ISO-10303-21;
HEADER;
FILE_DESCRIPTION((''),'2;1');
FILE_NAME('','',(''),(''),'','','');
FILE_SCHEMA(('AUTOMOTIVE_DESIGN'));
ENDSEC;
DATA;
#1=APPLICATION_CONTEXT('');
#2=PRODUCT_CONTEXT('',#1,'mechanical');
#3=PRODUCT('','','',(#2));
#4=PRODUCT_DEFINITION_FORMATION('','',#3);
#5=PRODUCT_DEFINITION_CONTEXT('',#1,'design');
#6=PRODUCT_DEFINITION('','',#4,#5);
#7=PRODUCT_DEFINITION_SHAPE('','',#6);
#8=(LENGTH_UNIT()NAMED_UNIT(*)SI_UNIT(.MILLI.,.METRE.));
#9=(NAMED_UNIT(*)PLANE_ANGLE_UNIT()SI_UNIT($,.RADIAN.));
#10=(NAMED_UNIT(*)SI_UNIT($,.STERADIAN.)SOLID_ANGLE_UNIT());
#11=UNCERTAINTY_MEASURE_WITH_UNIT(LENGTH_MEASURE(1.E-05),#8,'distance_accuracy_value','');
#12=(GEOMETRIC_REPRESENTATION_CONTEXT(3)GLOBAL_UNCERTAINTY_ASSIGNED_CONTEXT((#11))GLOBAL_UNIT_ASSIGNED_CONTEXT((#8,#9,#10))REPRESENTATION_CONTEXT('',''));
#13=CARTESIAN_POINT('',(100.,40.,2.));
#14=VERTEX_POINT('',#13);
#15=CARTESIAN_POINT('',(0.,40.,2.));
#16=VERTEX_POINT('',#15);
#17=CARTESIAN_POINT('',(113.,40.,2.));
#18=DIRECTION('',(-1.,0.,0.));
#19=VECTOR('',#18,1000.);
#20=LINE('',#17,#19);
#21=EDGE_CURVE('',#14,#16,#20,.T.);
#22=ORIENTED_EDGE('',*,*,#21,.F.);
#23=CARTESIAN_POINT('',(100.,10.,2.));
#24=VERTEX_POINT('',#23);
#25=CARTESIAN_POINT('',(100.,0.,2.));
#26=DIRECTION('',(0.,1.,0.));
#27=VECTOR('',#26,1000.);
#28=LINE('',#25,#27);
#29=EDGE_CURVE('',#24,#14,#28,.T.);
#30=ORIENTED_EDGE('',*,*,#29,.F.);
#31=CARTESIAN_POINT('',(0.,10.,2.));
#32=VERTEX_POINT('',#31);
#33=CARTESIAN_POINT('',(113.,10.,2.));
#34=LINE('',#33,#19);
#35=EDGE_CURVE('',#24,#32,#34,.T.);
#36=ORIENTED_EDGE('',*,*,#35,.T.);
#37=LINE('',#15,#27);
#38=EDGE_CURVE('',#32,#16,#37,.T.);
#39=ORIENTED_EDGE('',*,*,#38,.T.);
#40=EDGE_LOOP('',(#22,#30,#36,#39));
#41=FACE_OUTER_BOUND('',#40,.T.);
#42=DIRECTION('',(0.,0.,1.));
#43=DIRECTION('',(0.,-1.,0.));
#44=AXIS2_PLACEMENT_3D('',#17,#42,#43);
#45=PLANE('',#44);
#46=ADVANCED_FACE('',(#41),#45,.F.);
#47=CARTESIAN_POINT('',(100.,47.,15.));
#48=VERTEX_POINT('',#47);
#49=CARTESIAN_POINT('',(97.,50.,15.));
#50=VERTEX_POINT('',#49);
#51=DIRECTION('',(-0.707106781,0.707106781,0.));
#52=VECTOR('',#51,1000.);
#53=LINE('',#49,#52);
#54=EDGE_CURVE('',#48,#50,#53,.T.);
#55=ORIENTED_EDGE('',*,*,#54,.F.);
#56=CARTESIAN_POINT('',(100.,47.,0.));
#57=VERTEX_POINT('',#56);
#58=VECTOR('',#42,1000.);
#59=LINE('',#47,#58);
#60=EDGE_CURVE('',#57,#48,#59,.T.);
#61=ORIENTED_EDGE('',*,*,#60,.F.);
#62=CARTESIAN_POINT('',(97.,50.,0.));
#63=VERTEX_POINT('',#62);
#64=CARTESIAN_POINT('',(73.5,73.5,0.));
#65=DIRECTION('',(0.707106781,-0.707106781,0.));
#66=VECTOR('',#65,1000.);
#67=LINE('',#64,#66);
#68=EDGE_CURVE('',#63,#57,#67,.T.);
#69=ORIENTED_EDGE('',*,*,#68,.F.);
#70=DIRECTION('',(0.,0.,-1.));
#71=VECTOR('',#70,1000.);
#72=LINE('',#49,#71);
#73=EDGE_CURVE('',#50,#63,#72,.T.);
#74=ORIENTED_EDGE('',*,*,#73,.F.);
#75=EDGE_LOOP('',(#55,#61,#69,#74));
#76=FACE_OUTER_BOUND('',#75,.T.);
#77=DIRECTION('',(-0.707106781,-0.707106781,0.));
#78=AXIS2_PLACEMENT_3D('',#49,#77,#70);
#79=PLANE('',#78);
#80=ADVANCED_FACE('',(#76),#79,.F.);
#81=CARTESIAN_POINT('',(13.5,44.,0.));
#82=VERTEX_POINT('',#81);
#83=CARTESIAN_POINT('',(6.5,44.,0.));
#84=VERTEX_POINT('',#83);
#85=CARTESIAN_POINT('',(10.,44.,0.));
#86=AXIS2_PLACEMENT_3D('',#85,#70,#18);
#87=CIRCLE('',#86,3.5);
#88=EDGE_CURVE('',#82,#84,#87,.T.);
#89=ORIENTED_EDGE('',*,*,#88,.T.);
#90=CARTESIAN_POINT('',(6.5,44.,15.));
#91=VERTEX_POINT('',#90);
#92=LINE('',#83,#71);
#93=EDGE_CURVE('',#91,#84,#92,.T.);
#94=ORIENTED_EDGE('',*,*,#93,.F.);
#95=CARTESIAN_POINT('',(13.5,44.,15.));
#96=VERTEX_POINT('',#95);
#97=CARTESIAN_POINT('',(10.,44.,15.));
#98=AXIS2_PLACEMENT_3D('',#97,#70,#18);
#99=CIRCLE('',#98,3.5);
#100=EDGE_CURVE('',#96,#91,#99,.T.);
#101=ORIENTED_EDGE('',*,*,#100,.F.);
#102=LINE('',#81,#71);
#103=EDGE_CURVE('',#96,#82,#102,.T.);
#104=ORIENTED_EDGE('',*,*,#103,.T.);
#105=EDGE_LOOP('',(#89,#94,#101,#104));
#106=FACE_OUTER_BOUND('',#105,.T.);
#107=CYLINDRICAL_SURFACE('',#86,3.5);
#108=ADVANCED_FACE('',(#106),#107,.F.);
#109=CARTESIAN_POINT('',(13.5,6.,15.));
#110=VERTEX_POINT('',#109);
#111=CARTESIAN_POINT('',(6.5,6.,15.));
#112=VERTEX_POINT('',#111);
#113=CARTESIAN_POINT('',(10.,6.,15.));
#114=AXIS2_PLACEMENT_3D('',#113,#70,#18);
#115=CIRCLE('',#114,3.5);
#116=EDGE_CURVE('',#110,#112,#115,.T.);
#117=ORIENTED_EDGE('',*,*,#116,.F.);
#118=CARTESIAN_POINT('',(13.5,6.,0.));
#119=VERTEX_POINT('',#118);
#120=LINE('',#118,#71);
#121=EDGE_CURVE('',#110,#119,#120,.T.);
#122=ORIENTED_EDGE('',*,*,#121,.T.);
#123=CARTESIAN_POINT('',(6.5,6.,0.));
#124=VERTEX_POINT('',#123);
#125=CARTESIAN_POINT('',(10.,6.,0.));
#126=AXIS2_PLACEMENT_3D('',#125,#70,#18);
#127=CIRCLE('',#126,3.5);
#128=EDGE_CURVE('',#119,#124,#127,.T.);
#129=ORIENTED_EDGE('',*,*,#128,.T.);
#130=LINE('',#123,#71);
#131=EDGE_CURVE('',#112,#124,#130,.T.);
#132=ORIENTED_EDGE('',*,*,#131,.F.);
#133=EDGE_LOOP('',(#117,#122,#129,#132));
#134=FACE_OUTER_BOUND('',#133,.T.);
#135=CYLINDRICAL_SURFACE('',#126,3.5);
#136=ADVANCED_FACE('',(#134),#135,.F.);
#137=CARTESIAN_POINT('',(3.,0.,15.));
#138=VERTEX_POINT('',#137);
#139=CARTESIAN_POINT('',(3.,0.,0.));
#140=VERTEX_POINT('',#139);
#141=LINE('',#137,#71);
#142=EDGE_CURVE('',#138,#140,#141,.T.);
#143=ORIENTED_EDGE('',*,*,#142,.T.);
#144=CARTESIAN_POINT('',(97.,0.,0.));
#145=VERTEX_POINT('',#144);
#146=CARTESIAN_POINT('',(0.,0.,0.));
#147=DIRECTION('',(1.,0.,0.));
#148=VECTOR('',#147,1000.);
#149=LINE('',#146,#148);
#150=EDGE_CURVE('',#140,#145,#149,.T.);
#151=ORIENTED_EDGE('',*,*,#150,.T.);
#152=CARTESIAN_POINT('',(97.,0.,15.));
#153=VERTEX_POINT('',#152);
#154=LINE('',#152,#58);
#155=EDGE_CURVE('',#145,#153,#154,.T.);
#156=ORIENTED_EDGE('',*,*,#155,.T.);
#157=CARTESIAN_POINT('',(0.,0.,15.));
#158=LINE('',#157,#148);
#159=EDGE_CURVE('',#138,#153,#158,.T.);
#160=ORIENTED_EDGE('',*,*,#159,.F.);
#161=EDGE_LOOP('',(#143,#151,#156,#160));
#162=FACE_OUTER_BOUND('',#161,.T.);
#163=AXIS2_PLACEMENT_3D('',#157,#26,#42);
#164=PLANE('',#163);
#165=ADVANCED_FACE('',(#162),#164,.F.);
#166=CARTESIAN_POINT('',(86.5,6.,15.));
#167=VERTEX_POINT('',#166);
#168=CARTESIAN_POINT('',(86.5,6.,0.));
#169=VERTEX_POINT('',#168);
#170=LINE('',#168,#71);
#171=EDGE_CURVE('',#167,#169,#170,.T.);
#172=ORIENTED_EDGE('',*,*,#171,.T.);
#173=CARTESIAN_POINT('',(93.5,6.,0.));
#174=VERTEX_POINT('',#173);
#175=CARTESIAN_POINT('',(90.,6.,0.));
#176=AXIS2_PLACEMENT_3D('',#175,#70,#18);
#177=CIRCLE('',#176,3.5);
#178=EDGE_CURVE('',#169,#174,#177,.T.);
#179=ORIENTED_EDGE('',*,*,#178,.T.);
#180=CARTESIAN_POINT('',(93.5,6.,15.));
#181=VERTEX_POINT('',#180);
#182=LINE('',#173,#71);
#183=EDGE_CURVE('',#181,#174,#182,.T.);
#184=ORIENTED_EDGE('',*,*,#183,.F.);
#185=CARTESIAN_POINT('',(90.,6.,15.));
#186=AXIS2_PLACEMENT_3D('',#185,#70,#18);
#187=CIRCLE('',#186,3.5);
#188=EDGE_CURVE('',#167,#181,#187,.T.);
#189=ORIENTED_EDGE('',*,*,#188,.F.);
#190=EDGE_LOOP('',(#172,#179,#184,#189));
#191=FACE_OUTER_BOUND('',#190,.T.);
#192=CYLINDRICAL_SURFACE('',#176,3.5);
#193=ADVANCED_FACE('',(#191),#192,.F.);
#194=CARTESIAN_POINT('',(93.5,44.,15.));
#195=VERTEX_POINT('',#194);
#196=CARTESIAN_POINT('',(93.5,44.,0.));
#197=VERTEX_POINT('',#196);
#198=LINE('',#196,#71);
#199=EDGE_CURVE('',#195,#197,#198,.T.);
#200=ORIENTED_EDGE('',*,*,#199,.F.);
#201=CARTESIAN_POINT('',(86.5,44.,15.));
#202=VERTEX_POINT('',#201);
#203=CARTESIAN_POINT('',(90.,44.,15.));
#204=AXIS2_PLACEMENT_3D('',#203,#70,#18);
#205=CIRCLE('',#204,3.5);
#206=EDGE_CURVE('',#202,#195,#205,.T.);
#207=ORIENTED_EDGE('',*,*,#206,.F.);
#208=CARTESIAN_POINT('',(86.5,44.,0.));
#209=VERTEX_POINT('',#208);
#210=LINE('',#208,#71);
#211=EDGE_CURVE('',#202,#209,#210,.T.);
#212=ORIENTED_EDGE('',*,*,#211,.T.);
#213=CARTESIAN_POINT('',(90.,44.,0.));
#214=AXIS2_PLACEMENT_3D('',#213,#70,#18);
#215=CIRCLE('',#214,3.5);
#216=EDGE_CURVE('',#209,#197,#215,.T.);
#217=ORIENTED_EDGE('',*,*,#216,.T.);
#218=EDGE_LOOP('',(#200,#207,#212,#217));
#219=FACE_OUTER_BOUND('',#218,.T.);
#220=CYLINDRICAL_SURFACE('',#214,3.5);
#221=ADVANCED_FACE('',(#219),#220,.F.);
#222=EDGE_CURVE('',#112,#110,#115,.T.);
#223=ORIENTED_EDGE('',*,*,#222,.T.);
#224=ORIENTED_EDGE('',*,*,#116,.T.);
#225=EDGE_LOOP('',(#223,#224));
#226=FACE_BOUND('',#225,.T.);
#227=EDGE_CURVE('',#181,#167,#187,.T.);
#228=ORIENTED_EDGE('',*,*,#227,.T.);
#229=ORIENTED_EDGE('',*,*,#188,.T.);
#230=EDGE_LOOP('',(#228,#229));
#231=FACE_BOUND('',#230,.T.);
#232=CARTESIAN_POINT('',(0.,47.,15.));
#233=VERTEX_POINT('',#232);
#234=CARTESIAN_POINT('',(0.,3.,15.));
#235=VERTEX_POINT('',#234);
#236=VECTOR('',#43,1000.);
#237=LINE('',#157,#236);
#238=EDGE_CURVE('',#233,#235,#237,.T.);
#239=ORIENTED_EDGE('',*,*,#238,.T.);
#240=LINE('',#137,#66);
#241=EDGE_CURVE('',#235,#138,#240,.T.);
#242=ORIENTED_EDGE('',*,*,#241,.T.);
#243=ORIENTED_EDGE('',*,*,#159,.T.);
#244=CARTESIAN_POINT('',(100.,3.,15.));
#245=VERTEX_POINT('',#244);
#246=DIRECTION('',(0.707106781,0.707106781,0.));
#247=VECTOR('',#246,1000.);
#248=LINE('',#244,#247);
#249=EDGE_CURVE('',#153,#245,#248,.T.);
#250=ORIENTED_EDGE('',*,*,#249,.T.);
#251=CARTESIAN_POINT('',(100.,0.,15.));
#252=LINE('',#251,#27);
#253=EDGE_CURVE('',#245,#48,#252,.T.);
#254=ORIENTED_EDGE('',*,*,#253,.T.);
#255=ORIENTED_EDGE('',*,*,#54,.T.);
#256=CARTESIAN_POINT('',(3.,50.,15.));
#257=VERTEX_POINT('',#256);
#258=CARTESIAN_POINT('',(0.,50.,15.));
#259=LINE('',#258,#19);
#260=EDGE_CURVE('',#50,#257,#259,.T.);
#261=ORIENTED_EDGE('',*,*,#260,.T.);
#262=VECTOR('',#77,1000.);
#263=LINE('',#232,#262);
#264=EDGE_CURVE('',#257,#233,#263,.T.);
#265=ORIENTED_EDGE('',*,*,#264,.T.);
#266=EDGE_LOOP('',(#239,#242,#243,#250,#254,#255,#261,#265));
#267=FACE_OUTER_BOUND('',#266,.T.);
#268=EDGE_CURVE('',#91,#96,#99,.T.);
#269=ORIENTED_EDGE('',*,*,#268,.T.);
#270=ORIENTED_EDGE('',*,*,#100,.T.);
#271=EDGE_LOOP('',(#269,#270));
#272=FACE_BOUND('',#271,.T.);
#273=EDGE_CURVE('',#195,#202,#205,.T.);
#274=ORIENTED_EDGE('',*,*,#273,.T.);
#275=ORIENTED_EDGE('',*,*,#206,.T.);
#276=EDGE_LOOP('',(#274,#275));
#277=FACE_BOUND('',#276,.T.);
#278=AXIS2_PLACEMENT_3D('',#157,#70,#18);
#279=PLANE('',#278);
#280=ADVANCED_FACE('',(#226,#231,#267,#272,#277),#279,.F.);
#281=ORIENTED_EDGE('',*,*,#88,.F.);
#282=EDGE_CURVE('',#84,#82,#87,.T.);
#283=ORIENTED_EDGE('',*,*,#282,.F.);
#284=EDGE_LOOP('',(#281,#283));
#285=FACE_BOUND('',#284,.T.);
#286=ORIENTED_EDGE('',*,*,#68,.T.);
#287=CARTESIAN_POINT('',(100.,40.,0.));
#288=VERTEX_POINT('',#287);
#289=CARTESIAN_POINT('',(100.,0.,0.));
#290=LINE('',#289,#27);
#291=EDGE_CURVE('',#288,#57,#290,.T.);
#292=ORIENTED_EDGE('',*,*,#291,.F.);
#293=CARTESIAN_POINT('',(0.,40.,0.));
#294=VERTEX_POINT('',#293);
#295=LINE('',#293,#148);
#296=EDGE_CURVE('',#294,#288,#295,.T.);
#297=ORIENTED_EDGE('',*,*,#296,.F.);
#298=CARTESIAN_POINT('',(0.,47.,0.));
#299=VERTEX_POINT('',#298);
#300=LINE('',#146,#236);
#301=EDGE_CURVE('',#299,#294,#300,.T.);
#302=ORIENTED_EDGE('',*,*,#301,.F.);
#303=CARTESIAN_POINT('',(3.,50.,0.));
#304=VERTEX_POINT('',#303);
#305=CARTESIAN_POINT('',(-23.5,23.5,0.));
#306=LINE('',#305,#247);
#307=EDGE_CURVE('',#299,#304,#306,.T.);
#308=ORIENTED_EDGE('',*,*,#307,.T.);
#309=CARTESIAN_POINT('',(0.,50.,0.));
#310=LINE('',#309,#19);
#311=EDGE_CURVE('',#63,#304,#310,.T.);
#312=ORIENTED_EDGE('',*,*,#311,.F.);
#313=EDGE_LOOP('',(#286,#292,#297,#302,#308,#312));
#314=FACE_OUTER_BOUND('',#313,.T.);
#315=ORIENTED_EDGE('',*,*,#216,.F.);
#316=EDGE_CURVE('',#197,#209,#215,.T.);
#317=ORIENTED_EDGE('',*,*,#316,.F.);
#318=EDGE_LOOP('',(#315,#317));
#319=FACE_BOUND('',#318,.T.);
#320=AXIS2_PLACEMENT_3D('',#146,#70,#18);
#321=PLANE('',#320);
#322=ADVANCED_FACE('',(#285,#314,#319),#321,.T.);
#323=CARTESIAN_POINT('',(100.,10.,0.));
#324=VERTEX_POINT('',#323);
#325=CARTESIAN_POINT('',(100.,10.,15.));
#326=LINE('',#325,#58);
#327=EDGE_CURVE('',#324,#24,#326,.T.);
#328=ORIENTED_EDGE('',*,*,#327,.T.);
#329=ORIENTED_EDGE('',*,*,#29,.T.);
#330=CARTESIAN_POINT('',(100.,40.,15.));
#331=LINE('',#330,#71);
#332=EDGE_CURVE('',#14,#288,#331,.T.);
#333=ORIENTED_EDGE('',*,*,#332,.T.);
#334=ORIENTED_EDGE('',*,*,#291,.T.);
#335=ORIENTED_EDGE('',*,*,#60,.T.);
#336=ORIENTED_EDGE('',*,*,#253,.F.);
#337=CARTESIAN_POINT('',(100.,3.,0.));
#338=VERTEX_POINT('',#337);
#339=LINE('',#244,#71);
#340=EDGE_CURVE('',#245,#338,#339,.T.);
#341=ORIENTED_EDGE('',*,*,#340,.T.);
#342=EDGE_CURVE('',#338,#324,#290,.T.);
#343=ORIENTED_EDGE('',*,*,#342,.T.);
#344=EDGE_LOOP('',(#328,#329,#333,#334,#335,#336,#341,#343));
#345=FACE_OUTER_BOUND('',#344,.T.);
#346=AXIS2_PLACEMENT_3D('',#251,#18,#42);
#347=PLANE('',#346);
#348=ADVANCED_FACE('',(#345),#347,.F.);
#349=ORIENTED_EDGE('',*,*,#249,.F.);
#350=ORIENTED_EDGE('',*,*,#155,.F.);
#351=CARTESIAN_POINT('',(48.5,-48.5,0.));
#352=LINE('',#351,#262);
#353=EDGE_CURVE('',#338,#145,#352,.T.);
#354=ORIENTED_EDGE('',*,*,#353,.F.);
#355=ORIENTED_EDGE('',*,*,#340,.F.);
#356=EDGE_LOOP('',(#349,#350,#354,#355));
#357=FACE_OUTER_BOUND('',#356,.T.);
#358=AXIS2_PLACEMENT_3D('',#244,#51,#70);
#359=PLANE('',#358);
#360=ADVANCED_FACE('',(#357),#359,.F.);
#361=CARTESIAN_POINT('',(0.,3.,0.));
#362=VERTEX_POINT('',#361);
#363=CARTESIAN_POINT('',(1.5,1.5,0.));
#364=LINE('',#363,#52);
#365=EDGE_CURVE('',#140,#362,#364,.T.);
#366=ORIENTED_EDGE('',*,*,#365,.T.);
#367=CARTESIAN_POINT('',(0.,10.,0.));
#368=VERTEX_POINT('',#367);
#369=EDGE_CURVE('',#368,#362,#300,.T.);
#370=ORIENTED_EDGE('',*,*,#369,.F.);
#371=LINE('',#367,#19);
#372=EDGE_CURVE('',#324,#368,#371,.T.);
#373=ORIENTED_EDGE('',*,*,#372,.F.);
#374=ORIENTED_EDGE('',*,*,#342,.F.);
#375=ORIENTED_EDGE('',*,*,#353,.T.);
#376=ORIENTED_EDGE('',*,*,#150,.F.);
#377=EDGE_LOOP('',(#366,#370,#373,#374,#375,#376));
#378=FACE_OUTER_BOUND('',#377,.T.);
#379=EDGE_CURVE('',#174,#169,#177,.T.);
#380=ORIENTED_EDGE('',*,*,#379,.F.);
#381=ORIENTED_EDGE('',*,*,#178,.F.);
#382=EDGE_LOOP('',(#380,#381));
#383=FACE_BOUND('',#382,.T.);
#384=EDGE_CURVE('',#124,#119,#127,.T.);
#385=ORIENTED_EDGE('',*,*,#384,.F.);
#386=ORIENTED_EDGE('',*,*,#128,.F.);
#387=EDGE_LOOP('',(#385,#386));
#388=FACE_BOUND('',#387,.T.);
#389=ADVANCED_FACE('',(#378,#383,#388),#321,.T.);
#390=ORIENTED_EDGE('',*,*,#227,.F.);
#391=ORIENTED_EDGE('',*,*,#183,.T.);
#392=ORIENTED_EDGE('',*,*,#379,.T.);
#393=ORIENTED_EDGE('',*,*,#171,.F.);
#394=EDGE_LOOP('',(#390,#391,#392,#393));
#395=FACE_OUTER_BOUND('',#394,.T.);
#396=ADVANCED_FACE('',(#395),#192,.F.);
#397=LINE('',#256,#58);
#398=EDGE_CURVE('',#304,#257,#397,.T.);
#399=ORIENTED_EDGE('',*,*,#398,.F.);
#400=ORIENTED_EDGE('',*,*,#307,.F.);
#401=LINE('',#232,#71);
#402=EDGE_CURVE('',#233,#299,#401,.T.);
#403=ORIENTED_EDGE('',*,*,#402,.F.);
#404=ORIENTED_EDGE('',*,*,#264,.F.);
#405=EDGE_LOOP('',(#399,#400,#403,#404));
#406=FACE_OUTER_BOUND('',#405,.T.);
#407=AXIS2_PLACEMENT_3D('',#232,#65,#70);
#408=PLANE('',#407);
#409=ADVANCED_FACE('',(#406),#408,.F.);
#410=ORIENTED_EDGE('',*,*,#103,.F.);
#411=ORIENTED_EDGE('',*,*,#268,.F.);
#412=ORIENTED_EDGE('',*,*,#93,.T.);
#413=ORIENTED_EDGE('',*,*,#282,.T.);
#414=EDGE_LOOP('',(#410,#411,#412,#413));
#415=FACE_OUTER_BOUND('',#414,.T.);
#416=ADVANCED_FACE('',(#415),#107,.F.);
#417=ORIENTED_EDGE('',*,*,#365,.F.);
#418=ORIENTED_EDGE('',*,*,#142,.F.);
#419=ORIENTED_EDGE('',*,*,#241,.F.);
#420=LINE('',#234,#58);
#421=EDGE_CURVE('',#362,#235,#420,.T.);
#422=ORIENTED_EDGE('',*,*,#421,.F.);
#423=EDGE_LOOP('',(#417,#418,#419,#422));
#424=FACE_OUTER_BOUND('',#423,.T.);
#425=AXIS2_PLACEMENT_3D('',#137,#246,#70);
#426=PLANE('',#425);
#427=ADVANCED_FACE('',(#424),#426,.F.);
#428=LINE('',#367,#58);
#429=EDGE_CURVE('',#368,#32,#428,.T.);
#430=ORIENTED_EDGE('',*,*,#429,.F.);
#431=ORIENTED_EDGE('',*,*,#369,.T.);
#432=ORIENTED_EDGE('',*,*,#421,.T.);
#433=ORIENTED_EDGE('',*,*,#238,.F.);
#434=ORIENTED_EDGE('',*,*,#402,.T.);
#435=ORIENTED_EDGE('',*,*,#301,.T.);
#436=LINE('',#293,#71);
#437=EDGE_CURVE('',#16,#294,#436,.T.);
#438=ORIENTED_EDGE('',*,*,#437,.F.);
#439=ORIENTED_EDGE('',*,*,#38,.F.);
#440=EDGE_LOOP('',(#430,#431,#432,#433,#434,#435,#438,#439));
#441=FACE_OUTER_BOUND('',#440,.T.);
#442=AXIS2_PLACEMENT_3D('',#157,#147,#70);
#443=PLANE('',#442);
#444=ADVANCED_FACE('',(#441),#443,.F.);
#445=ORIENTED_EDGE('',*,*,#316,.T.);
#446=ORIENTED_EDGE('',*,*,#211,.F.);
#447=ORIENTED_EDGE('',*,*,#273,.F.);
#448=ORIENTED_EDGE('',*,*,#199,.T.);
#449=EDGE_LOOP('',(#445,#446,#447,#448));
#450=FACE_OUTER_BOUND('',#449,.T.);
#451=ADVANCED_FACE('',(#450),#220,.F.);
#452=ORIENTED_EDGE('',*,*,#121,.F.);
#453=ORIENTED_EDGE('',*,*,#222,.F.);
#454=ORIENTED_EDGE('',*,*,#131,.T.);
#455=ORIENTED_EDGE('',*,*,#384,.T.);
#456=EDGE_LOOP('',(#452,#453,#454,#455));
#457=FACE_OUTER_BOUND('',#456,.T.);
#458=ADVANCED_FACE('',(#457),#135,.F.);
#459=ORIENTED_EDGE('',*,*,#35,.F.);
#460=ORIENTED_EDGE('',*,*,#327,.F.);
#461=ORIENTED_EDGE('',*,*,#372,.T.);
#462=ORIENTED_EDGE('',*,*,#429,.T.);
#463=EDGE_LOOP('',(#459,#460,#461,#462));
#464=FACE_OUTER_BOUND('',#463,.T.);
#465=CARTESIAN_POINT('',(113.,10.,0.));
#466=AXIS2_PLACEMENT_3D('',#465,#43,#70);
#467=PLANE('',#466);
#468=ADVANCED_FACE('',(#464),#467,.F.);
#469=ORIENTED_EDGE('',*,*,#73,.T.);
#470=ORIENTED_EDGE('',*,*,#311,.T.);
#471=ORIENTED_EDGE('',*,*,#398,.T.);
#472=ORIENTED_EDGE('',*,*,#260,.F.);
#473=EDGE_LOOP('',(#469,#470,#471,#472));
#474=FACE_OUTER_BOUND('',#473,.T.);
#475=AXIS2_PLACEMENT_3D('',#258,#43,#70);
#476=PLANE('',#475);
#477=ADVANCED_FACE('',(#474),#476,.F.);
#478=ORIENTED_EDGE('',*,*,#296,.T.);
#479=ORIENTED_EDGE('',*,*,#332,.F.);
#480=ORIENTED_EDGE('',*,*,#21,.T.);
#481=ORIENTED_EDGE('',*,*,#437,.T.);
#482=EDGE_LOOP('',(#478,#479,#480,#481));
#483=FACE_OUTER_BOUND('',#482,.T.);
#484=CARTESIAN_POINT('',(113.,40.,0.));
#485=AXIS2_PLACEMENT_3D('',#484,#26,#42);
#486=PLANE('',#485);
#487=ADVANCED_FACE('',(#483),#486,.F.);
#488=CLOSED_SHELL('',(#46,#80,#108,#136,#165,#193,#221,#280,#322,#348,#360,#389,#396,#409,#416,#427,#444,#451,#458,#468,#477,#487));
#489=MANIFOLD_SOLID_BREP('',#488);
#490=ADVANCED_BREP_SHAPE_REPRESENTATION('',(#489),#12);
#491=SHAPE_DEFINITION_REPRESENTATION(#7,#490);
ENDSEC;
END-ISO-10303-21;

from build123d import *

# Parameters (mm, degrees)
SKETCH_1_W            = 100
SKETCH_1_H            = 50
EXTRUDE_1_DEPTH       = 15
HOLE_WIZARD_7_0_7_1_D = 7
CHAMFER_1_SIZE        = 3
SKETCH_6_W            = 2
SKETCH_6_H            = 30
CUT_EXTRUDE_1_DEPTH   = 113


with BuildPart() as part:
    # 草图1 → 凸台-拉伸1 (new body)
    with BuildSketch(Plane.XY):
        with Locations((50, 25)):
            Rectangle(SKETCH_1_W, SKETCH_1_H)
    extrude(amount=EXTRUDE_1_DEPTH)

    # Ø7.0 (7) 直径孔1 (through all)
    with Locations(Plane(origin=(0, 0, 0), x_dir=(-1, 0, 0), z_dir=(0, 0, -1))):
        with Locations((-10, 44), (-10, 6), (-90, 44), (-90, 6)):
            Hole(HOLE_WIZARD_7_0_7_1_D / 2)

    # 倒角1
    chamfer_1_edges = [part.edges().sort_by_distance(p)[0] for p in [
        (0, 50, 7.5),
        (100, 50, 7.5),
        (100, 0, 7.5),
        (0, 0, 7.5),
    ]]
    chamfer(chamfer_1_edges, length=CHAMFER_1_SIZE)

    # 草图6 → 切除-拉伸1 (cut)
    with BuildSketch(Plane.ZY):
        with Locations((1, 25)):
            Rectangle(SKETCH_6_W, SKETCH_6_H)
    extrude(amount=-CUT_EXTRUDE_1_DEPTH, mode=Mode.SUBTRACT)


solid = part.part
